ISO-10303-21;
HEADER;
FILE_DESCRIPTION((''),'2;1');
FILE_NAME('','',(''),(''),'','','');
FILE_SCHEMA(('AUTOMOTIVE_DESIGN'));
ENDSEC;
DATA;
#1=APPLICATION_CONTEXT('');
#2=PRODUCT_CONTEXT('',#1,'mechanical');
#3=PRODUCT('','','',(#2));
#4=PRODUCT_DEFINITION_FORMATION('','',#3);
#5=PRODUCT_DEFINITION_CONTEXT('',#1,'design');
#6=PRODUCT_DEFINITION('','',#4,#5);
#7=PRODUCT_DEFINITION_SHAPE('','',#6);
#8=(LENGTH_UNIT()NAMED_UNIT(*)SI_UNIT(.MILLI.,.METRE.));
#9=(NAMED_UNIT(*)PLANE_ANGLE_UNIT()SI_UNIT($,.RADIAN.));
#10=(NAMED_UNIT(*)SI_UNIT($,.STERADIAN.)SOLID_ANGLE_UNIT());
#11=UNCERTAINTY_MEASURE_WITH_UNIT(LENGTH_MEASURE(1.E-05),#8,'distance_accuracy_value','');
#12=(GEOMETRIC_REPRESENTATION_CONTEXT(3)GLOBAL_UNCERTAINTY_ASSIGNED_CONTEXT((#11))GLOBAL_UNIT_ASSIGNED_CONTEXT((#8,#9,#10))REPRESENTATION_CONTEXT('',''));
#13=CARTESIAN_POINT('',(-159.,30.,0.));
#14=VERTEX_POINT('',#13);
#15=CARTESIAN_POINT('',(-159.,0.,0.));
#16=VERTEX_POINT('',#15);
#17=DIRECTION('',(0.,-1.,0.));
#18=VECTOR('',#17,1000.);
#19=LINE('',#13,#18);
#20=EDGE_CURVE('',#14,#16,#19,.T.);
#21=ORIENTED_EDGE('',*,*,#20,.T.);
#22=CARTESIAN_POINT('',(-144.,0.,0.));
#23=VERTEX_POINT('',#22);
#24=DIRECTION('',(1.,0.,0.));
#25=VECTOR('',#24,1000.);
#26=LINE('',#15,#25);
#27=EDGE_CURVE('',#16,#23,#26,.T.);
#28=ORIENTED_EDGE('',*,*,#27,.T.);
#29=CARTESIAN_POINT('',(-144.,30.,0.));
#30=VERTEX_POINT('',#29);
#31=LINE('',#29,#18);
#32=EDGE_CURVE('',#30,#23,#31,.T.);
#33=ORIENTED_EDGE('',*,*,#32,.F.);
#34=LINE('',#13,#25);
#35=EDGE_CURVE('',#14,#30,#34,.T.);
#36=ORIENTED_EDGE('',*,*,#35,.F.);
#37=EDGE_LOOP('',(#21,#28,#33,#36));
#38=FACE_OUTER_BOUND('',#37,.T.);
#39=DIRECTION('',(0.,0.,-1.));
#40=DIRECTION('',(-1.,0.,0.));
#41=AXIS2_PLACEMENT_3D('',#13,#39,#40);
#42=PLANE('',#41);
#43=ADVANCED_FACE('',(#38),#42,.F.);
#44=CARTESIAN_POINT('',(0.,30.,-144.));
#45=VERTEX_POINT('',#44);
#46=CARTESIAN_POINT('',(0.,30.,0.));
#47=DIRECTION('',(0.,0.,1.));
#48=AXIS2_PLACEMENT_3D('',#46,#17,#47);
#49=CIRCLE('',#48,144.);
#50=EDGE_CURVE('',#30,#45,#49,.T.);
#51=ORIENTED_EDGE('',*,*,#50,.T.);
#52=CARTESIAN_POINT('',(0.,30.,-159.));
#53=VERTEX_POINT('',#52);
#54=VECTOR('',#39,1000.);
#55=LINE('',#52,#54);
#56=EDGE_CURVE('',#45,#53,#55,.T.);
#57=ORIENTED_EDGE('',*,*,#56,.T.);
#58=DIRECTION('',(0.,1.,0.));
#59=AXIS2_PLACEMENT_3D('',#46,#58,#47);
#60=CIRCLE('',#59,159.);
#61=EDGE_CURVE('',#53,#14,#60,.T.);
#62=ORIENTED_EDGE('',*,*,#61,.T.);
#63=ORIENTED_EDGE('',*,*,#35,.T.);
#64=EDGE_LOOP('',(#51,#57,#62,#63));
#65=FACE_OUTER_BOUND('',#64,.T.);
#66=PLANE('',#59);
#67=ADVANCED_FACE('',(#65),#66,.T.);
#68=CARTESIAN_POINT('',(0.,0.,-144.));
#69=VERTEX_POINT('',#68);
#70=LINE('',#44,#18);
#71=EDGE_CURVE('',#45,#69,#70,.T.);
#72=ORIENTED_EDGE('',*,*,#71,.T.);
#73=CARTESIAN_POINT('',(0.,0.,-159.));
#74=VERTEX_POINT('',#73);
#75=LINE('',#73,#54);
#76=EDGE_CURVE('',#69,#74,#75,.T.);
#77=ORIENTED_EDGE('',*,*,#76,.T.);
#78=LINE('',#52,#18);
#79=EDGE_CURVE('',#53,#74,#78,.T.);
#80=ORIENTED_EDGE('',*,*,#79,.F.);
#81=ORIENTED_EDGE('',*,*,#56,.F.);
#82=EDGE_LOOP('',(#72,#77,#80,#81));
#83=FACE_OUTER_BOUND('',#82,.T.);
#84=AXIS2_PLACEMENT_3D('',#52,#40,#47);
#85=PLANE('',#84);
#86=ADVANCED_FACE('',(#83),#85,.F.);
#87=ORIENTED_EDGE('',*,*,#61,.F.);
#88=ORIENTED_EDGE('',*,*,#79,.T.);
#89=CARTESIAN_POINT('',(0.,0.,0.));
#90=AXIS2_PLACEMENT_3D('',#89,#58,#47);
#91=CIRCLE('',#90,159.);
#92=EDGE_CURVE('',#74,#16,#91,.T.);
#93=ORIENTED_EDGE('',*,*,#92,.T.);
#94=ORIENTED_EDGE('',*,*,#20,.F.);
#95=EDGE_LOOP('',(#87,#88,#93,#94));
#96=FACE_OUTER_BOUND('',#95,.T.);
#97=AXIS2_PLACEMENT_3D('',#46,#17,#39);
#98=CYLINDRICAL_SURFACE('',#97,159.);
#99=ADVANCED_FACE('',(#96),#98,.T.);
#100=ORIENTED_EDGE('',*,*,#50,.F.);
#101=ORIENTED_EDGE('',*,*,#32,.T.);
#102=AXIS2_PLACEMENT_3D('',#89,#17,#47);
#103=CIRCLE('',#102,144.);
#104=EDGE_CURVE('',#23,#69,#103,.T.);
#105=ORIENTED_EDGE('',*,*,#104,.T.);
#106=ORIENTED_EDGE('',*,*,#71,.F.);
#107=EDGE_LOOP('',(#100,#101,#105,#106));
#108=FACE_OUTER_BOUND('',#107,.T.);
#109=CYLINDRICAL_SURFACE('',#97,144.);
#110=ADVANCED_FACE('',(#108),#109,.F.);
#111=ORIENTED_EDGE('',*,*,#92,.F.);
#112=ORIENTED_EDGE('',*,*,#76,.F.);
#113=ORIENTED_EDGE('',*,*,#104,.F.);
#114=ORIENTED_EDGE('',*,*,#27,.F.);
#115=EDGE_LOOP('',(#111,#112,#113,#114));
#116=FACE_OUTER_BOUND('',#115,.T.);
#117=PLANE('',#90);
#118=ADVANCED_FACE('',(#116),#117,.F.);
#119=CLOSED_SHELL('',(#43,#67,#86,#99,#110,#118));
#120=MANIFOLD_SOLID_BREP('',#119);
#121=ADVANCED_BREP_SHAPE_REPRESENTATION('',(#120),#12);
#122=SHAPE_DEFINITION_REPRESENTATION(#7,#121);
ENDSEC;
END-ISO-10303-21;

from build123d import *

# Parameters (mm, degrees)
EXTRUDE_1_DEPTH = 30


with BuildPart() as part:
    # 草图1 → 凸台-拉伸1 (new body)
    with BuildSketch(Plane(origin=(0, 0, 0), x_dir=(1, 0, 0), z_dir=(0, 1, 0))):
        with BuildLine():
            Line((-159, 0), (-144, 0))
            ThreePointArc((-144, 0), (-101.823376491, 101.823376491), (0, 144))
            Line((0, 144), (0, 159))
            ThreePointArc((0, 159), (-112.429978209, 112.429978209), (-159, 0))
        make_face()
    extrude(amount=EXTRUDE_1_DEPTH)


solid = part.part
